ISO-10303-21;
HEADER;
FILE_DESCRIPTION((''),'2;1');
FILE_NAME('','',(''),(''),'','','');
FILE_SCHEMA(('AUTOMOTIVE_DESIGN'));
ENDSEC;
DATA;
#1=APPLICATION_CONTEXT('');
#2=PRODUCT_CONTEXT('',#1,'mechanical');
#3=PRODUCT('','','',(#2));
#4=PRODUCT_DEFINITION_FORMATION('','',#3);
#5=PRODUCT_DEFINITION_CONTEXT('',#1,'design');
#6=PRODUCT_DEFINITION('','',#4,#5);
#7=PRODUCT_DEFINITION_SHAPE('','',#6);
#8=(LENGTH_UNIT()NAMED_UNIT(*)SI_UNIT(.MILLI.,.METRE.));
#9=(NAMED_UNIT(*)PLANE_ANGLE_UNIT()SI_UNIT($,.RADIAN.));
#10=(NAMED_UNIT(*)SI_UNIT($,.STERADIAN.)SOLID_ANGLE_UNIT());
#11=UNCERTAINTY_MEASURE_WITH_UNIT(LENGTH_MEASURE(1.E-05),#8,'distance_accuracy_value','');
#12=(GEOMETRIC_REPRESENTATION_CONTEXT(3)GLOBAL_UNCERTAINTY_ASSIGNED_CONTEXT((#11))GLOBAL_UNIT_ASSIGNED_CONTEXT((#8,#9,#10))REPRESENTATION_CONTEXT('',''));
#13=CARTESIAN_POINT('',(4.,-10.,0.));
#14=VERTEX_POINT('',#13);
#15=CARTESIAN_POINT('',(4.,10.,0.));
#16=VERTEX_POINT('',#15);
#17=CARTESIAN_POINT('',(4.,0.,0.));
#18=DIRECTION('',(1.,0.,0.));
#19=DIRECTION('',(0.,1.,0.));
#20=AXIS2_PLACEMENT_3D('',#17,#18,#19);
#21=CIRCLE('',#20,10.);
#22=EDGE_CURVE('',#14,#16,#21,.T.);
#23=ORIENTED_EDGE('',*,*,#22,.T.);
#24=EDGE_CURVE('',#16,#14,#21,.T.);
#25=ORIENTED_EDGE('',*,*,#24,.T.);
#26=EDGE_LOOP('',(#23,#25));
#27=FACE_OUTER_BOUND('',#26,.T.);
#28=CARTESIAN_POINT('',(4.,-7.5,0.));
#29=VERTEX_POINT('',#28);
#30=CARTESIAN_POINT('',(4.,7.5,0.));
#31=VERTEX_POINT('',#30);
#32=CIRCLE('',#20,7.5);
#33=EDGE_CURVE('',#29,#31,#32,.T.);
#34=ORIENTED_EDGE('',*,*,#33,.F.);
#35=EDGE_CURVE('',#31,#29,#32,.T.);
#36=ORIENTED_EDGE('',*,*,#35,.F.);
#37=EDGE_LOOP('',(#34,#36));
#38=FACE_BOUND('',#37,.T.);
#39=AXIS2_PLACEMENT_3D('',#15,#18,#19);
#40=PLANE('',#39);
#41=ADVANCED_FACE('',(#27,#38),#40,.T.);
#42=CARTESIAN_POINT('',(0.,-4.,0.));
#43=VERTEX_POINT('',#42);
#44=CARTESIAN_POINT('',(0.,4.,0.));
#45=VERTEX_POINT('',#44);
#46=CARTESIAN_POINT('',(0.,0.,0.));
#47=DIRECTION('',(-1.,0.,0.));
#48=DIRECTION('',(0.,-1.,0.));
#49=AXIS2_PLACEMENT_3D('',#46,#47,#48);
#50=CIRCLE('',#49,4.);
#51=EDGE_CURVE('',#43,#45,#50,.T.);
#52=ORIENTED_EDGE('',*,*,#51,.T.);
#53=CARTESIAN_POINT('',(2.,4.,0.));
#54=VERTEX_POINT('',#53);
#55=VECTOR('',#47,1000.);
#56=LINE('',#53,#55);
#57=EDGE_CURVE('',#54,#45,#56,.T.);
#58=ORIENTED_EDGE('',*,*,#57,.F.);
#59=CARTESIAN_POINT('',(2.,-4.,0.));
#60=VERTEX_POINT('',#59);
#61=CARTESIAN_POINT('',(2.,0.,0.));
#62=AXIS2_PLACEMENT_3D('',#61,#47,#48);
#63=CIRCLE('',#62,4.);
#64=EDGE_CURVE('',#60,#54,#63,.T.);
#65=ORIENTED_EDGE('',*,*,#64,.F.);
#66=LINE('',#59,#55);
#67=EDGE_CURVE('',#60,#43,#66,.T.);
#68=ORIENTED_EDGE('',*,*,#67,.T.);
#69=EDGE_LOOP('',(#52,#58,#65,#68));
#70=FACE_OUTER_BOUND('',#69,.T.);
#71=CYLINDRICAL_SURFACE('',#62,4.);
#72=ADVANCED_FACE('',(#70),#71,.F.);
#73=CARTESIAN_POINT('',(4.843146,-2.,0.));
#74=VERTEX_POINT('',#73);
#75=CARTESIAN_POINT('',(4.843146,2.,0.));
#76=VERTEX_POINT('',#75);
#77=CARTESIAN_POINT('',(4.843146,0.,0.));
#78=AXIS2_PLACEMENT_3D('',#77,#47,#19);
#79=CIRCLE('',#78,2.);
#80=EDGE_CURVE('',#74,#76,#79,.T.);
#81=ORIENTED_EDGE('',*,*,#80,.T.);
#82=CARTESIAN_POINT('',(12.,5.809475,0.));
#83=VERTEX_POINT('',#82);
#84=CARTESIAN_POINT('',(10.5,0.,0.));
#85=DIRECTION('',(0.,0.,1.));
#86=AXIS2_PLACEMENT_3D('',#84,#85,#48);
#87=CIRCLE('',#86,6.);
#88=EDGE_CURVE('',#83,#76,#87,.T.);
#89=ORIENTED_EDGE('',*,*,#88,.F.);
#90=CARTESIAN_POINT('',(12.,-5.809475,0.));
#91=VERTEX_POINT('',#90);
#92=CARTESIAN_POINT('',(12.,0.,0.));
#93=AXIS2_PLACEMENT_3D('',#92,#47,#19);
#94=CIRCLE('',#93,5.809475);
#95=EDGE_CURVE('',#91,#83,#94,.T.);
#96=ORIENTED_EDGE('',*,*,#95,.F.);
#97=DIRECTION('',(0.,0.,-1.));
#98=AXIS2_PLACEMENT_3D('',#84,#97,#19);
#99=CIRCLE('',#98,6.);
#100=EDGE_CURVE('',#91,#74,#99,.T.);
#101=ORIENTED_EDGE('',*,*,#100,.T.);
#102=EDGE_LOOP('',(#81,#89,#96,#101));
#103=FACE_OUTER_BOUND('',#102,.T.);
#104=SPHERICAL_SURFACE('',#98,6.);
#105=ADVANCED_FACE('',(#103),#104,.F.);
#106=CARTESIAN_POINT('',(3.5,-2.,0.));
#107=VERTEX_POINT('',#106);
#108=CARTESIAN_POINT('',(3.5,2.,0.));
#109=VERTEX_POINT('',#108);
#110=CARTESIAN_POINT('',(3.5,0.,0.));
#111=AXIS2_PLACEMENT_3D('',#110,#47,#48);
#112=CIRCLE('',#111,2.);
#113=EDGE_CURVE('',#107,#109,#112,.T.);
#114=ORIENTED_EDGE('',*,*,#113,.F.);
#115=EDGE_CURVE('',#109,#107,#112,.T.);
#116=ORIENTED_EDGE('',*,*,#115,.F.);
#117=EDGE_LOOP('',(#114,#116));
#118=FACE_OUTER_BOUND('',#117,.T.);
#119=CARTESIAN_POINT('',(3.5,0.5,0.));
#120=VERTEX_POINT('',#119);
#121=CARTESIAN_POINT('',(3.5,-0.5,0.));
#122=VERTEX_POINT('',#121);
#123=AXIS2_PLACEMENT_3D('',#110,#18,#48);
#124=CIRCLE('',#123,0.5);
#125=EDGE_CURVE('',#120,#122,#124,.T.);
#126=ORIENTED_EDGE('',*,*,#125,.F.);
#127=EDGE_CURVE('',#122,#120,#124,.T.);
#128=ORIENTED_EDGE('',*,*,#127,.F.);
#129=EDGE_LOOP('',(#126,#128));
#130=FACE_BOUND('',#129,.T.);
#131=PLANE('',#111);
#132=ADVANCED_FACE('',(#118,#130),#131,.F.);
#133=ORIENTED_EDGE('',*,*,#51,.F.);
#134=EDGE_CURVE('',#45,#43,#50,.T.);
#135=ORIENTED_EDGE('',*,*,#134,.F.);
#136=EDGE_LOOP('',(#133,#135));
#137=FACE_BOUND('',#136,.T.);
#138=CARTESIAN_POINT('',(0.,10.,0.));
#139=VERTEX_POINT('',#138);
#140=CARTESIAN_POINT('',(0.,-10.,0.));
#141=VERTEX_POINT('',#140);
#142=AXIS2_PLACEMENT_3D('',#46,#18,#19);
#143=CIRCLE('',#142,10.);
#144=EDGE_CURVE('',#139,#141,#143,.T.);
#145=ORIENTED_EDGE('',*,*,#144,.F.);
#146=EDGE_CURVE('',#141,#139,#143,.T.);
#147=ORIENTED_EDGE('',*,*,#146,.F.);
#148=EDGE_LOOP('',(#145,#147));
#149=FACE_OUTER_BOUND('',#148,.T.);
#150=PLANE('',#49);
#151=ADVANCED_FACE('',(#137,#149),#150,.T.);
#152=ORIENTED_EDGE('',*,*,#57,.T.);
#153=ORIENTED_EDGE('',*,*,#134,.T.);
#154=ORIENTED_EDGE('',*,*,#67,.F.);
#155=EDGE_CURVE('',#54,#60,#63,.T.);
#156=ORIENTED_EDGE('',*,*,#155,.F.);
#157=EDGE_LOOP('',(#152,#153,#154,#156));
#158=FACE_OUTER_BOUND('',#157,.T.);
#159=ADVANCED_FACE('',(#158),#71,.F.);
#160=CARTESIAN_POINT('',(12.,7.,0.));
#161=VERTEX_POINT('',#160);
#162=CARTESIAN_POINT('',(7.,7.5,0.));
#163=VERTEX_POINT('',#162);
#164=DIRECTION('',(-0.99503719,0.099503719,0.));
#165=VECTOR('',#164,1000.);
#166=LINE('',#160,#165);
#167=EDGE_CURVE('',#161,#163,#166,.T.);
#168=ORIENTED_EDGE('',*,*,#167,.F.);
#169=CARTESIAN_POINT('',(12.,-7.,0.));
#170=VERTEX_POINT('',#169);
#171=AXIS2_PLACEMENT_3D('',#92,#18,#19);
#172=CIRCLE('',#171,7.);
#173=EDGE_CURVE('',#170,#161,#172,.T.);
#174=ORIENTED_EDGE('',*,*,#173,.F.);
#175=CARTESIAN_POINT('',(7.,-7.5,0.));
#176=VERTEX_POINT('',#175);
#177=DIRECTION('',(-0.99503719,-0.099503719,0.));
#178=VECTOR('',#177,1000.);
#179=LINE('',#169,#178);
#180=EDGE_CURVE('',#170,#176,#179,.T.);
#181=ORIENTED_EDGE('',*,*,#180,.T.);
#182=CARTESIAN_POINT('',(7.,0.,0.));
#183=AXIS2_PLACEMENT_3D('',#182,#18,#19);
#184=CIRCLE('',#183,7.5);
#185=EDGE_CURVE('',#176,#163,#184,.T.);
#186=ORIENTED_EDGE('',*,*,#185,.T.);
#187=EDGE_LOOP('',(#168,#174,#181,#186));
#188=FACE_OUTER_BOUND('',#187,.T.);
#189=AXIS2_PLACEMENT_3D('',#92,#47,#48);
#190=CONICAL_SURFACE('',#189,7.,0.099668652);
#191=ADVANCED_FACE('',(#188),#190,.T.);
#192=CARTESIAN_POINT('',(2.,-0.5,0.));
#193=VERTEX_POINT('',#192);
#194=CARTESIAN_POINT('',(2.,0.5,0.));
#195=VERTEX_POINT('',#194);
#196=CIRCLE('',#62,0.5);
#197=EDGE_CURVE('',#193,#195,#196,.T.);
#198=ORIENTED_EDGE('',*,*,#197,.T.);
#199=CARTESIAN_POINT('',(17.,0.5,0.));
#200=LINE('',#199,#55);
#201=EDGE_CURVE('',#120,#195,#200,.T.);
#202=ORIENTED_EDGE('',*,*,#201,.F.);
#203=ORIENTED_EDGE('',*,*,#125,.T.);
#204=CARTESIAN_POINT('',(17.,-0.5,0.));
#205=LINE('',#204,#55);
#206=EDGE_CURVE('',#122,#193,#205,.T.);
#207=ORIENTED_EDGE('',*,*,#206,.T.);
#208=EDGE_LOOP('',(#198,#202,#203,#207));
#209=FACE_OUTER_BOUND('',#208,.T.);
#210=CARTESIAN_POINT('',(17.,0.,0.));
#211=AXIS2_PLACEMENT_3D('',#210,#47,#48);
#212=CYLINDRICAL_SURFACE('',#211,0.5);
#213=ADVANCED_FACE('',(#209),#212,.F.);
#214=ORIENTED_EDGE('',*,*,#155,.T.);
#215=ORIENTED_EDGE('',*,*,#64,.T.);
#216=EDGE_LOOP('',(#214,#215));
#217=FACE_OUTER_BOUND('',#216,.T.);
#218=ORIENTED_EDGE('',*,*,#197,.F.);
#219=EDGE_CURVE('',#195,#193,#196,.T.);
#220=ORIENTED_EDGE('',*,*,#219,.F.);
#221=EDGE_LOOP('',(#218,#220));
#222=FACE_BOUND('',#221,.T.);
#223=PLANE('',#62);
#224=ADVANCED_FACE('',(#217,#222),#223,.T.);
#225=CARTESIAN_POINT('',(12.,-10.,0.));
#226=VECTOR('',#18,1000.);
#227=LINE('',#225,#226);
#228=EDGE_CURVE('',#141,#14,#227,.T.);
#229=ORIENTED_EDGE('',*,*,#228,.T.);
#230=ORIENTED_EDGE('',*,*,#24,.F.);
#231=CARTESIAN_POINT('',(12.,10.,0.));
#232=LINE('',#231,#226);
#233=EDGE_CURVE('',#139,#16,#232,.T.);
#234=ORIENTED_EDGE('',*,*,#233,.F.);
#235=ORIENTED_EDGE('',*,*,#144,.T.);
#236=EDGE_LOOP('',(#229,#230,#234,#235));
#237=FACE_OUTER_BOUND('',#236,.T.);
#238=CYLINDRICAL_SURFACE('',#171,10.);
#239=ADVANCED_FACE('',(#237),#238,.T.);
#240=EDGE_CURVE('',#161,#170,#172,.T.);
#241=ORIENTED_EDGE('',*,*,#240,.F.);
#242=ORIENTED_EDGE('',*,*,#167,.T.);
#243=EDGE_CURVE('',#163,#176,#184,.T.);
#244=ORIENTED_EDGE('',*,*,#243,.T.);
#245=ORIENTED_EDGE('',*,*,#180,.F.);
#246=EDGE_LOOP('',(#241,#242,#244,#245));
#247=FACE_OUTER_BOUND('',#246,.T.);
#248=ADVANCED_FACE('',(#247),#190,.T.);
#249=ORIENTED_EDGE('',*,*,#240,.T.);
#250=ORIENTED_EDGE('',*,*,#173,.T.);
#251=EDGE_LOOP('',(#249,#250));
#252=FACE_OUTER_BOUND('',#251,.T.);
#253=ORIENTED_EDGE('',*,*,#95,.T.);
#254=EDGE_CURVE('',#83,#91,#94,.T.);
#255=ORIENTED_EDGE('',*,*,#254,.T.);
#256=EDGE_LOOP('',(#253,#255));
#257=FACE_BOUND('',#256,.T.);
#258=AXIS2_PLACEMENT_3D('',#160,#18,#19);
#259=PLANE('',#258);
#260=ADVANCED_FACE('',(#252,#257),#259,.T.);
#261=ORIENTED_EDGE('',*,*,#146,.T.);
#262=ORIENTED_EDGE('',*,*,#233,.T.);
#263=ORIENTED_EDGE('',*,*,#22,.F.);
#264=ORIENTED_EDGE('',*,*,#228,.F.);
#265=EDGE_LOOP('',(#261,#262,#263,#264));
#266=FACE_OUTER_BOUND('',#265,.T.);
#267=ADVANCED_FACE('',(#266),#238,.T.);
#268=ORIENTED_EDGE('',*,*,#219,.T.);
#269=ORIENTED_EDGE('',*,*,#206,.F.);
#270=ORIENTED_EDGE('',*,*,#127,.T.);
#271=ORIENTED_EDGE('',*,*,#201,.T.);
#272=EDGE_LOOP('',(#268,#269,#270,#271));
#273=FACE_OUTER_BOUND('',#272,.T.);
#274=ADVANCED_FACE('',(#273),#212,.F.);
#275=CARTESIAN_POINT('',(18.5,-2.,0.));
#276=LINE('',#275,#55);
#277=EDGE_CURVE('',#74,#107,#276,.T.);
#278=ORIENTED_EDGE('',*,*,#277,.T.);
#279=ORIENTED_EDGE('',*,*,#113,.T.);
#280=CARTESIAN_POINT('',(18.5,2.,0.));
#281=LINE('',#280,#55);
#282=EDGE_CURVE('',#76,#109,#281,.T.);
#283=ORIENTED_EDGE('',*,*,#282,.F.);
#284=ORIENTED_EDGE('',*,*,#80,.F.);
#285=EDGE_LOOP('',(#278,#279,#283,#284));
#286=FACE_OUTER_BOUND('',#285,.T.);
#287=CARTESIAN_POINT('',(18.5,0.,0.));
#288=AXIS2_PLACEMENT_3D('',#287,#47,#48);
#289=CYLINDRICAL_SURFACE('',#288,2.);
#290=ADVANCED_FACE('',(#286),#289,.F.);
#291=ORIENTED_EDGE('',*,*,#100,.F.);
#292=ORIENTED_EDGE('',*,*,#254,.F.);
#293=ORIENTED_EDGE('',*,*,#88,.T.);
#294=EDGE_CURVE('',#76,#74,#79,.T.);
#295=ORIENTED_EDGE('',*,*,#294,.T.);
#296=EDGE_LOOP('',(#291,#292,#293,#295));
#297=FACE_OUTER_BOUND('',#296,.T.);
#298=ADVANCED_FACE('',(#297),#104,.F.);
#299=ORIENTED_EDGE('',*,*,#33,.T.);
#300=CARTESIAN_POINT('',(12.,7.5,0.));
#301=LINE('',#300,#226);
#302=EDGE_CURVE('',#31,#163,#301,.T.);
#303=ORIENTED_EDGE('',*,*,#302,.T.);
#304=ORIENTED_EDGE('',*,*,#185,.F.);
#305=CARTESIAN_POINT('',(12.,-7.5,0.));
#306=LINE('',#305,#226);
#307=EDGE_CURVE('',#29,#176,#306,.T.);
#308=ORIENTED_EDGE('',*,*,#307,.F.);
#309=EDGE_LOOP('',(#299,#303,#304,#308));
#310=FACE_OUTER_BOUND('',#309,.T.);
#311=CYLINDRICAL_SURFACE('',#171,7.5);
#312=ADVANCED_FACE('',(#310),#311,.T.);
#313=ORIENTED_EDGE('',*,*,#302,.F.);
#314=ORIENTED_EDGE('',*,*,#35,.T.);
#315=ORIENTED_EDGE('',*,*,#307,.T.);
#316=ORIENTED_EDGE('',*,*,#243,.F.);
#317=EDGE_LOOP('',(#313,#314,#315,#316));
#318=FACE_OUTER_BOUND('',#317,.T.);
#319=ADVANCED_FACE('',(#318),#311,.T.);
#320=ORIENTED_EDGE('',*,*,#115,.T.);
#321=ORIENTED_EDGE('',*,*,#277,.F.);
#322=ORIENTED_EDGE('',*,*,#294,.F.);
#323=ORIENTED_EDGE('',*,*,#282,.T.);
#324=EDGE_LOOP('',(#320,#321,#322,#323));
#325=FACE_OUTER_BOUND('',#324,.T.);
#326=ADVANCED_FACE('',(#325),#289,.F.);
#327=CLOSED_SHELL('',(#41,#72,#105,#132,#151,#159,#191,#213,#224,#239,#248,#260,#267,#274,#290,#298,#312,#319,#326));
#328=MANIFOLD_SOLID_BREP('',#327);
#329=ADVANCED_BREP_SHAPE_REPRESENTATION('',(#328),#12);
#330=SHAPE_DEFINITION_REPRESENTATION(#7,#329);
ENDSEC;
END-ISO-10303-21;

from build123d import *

# Parameters (mm, degrees)
SKETCH2_R          = 4
CUT_EXTRUDE1_DEPTH = 2
SKETCH3_R          = 0.5
CUT_EXTRUDE2_DEPTH = 15
CUT_EXTRUDE3_START = -3.5
SKETCH5_R          = 2
CUT_EXTRUDE3_DEPTH = 15


with BuildPart() as part:
    # Sketch1 → Revolve1 (revolve)
    with BuildSketch(Plane.XY):
        Polygon((0, 0), (0, 10), (4, 10), (4, 7.5), (7, 7.5), (12, 7), (12, 0), align=None)
    revolve(axis=Axis((12, 0, 0), (-1, 0, 0)))

    # Sketch2 → Cut-Extrude1 (cut)
    with BuildSketch(Plane.ZY):
        with Locations(Location((0, 0, 0), (0, 0, 270))):
            Circle(SKETCH2_R)
    extrude(amount=-CUT_EXTRUDE1_DEPTH, mode=Mode.SUBTRACT)

    # Sketch3 → Cut-Extrude2 (cut)
    with BuildSketch(Plane.ZY.offset(-2)):
        with Locations(Location((0, 0, 0), (0, 0, 270))):
            Circle(SKETCH3_R)
    extrude(amount=-CUT_EXTRUDE2_DEPTH, mode=Mode.SUBTRACT)

    # Sketch5 → Cut-Extrude3 (cut)
    with BuildSketch(Plane.ZY.offset(CUT_EXTRUDE3_START)):
        with Locations(Location((0, 0, 0), (0, 0, 270))):
            Circle(SKETCH5_R)
    extrude(amount=-CUT_EXTRUDE3_DEPTH, mode=Mode.SUBTRACT)

    # Sketch6 → Cut-Revolve1 (revolve, cut)
    with BuildSketch(Plane.XY):
        with BuildLine():
            Line((4.5, 0), (16.5, 0))
            ThreePointArc((16.5, 0), (10.5, 6), (4.5, 0))
        make_face()
    revolve(axis=Axis((4.5, 0, 0), (1, 0, 0)), mode=Mode.SUBTRACT)


solid = part.part
